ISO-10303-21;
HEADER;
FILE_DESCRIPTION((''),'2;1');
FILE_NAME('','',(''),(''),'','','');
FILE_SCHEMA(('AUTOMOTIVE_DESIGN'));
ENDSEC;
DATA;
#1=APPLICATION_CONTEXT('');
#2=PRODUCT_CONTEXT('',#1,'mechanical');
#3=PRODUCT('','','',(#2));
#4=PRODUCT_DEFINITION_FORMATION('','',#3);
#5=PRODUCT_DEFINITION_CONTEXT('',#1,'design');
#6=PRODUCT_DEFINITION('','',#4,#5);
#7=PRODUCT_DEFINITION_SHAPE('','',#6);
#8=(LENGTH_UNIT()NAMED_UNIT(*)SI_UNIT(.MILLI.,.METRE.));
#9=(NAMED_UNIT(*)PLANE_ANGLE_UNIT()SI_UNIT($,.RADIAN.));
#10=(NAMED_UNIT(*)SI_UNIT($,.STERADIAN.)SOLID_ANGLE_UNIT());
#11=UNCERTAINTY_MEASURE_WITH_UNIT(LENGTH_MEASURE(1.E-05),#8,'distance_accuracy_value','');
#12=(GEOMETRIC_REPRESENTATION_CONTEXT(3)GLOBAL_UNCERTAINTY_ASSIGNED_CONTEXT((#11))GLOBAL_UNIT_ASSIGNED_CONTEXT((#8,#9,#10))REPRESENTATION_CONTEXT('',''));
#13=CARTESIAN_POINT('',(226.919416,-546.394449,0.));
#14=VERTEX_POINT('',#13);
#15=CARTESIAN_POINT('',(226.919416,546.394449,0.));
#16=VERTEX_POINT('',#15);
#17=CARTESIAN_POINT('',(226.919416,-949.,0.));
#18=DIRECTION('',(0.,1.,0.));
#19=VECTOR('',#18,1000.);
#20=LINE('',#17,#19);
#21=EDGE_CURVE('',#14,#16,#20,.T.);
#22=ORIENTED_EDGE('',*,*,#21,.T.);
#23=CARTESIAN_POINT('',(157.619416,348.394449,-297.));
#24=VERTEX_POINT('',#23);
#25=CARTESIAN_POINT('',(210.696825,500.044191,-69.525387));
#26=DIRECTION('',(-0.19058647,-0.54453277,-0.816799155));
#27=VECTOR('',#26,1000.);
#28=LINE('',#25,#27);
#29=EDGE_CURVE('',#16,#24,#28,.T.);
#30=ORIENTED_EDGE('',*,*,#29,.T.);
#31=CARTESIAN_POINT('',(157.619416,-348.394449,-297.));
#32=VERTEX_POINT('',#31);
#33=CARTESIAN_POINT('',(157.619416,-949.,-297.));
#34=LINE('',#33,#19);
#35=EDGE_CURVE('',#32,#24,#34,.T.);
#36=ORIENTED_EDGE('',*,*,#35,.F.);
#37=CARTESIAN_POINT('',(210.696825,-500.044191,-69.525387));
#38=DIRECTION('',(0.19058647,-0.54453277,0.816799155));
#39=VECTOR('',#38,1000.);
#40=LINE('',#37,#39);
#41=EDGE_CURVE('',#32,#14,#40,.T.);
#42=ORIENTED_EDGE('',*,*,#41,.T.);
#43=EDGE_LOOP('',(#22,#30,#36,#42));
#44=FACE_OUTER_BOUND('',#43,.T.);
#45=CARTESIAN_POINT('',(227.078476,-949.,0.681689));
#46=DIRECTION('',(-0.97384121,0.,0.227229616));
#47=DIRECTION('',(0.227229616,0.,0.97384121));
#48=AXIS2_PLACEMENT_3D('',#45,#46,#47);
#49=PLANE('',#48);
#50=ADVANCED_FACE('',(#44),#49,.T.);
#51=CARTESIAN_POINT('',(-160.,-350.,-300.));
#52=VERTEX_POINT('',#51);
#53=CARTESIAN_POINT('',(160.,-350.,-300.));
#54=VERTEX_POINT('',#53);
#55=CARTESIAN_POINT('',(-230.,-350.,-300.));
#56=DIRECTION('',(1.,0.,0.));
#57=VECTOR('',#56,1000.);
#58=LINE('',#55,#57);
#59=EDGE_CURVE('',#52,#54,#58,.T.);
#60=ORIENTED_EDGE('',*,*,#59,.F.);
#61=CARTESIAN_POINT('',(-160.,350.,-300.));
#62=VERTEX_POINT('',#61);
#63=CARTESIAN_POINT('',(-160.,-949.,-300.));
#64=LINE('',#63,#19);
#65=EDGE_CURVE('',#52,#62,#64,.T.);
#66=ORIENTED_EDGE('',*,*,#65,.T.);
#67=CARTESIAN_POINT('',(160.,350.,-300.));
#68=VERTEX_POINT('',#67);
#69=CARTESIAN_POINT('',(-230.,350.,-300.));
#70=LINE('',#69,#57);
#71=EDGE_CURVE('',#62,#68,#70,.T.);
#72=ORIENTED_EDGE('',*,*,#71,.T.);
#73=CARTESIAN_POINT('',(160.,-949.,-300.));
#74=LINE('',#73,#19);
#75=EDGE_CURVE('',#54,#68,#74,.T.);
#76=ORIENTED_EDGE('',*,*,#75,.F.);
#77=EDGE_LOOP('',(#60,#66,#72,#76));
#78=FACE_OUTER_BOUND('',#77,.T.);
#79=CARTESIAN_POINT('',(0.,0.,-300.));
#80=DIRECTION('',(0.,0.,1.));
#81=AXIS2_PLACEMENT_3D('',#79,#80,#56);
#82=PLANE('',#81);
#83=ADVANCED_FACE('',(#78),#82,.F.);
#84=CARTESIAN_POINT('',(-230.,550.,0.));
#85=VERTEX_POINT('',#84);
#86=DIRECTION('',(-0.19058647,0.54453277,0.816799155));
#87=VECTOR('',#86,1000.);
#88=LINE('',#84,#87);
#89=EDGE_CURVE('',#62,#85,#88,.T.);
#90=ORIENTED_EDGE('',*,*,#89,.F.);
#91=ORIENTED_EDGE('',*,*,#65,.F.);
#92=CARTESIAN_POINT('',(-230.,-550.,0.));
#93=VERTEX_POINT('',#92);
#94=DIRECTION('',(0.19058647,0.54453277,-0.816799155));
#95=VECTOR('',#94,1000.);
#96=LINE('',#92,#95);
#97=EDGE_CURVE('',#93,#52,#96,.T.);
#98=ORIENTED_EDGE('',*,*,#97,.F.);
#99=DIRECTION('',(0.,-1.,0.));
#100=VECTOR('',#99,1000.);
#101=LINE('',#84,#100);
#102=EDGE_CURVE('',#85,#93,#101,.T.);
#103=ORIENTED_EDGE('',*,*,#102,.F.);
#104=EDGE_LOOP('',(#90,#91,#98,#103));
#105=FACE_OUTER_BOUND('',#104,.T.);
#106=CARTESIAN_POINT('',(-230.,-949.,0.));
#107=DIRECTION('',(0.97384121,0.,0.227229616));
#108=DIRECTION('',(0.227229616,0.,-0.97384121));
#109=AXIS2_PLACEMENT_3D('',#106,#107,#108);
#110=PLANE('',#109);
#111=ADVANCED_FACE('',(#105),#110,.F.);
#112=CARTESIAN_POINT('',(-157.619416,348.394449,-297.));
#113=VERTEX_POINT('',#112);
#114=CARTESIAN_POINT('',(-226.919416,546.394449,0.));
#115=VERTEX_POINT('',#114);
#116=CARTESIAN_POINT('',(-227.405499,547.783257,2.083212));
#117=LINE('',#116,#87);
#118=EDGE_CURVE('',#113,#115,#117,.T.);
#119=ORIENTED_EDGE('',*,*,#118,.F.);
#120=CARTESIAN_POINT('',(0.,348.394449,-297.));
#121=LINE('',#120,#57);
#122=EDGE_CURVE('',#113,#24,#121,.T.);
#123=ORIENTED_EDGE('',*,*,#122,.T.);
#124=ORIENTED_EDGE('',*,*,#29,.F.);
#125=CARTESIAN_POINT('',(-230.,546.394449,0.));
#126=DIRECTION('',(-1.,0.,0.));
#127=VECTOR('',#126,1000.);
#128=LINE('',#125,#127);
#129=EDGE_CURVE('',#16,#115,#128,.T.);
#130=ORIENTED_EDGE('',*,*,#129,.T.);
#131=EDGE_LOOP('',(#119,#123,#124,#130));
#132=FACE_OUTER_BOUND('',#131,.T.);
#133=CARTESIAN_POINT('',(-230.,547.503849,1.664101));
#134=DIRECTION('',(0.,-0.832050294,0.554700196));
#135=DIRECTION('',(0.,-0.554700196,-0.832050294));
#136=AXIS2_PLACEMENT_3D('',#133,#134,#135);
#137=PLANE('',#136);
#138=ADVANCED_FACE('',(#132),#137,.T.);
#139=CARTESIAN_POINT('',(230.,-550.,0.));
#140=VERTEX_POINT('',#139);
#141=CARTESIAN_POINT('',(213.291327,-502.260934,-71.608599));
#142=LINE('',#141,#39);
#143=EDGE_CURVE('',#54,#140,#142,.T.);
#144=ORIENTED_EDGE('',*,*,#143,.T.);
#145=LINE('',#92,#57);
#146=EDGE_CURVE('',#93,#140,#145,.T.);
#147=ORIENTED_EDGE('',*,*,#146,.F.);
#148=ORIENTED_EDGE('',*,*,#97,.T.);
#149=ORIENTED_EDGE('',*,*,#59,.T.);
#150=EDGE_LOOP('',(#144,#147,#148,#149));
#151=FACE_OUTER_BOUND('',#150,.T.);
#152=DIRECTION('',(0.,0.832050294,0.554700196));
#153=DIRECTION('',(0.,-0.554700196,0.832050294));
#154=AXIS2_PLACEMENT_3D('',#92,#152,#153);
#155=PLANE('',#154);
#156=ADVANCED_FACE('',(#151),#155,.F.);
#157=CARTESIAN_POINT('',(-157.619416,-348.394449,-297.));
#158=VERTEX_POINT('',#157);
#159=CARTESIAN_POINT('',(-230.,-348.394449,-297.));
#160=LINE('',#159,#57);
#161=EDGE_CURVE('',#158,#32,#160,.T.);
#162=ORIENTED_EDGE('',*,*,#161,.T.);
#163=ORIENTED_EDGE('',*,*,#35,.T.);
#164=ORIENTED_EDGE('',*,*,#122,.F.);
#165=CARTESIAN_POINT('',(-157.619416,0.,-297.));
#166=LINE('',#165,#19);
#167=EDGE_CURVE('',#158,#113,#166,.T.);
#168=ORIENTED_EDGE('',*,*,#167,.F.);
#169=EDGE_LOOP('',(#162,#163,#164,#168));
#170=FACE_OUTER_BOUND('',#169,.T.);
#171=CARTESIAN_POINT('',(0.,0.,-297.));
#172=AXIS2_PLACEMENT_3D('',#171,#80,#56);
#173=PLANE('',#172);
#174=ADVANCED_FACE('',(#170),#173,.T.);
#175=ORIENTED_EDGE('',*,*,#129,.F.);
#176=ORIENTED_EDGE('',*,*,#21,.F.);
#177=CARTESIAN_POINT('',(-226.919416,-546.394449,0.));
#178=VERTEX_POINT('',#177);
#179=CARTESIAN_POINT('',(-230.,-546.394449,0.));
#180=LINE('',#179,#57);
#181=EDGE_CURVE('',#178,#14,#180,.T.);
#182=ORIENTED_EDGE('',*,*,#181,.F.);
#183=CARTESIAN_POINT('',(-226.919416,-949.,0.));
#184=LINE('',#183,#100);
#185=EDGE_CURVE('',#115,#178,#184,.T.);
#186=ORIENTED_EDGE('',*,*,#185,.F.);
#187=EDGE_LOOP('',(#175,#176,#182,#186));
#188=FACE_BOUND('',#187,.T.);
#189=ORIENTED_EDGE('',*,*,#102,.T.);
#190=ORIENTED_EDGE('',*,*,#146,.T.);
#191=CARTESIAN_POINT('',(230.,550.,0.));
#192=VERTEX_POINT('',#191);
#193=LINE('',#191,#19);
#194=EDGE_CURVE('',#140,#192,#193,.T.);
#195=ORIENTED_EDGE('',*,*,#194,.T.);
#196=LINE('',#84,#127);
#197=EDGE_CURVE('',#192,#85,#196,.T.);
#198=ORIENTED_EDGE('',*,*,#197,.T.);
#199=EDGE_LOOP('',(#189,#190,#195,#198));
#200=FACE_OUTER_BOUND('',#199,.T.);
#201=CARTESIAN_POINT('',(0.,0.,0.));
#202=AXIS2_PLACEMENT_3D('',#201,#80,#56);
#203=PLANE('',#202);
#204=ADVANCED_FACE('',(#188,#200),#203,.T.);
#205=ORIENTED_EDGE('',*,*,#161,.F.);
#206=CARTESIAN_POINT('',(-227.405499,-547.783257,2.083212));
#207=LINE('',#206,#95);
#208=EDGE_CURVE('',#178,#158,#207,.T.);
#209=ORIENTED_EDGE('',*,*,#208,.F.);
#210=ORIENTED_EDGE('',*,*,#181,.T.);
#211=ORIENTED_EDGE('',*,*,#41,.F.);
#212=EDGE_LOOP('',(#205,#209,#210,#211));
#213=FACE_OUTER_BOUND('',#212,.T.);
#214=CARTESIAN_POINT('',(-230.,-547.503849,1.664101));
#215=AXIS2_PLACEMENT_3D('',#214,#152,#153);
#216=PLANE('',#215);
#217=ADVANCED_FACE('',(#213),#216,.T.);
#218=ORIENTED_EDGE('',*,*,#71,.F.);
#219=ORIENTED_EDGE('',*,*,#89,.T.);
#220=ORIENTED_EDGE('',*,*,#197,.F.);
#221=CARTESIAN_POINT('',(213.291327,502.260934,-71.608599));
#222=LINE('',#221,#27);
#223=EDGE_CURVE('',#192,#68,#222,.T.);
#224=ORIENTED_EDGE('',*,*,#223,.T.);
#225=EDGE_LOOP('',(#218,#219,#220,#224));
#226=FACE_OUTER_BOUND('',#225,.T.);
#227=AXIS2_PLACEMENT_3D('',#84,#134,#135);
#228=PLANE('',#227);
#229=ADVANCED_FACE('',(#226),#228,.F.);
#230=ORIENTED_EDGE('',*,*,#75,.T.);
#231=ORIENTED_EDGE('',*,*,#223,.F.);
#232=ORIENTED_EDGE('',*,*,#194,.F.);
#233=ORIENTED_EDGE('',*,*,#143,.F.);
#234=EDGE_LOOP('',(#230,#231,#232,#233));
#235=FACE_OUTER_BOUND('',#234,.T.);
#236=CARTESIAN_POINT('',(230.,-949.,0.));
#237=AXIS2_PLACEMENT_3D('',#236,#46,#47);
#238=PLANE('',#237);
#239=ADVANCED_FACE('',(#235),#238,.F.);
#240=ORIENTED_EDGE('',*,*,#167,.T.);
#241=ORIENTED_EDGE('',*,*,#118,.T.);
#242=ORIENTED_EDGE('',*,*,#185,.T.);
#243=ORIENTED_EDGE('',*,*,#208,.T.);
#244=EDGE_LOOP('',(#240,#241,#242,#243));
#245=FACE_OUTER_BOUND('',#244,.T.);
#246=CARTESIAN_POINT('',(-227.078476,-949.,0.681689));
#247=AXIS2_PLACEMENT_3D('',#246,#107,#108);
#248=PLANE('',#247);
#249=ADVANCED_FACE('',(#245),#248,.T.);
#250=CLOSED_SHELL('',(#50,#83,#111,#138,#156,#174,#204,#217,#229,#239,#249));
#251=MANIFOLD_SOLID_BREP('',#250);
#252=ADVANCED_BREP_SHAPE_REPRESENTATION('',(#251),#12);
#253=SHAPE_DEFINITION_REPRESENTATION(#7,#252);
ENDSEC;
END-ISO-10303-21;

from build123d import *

# Parameters (mm, degrees)
SKETCH1_W           = 460
SKETCH1_H           = 1100
BOSS_EXTRUDE1_DEPTH = 300
CUT_EXTRUDE1_DEPTH  = 778.238702073
CUT_EXTRUDE3_DEPTH  = 949
SHELL1_T            = -3


with BuildPart() as part:
    # Sketch1 → Boss-Extrude1 (new body)
    with BuildSketch(Plane.XY):
        Rectangle(SKETCH1_W, SKETCH1_H)
    extrude(amount=-BOSS_EXTRUDE1_DEPTH)

    # Sketch3 → Cut-Extrude1 (cut, through all)
    with BuildSketch(Plane(origin=(230, 0, 0), x_dir=(0, 0, -1), z_dir=(1, 0, 0))):
        Polygon((0, 550), (300, 350), (300, 550), align=None)
        Polygon((300, -550), (0, -550), (300, -350), align=None)
    extrude(amount=-CUT_EXTRUDE1_DEPTH, mode=Mode.SUBTRACT)

    # Sketch6 → Cut-Extrude3 (cut, symmetric)
    with BuildSketch(Plane(origin=(0, 0, 0), x_dir=(1, 0, 0), z_dir=(0, 1, 0))):
        Polygon((-230, 0), (-160, 300), (-230, 300), align=None)
        Polygon((230, 300), (230, 0), (160, 300), align=None)
    extrude(amount=CUT_EXTRUDE3_DEPTH, both=True, mode=Mode.SUBTRACT)

    # Shell1
    shell1_openings = [part.faces().sort_by_distance(p)[0] for p in [
        (0, 0, 0),
    ]]
    offset(amount=SHELL1_T, openings=shell1_openings, kind=Kind.INTERSECTION)


solid = part.part
